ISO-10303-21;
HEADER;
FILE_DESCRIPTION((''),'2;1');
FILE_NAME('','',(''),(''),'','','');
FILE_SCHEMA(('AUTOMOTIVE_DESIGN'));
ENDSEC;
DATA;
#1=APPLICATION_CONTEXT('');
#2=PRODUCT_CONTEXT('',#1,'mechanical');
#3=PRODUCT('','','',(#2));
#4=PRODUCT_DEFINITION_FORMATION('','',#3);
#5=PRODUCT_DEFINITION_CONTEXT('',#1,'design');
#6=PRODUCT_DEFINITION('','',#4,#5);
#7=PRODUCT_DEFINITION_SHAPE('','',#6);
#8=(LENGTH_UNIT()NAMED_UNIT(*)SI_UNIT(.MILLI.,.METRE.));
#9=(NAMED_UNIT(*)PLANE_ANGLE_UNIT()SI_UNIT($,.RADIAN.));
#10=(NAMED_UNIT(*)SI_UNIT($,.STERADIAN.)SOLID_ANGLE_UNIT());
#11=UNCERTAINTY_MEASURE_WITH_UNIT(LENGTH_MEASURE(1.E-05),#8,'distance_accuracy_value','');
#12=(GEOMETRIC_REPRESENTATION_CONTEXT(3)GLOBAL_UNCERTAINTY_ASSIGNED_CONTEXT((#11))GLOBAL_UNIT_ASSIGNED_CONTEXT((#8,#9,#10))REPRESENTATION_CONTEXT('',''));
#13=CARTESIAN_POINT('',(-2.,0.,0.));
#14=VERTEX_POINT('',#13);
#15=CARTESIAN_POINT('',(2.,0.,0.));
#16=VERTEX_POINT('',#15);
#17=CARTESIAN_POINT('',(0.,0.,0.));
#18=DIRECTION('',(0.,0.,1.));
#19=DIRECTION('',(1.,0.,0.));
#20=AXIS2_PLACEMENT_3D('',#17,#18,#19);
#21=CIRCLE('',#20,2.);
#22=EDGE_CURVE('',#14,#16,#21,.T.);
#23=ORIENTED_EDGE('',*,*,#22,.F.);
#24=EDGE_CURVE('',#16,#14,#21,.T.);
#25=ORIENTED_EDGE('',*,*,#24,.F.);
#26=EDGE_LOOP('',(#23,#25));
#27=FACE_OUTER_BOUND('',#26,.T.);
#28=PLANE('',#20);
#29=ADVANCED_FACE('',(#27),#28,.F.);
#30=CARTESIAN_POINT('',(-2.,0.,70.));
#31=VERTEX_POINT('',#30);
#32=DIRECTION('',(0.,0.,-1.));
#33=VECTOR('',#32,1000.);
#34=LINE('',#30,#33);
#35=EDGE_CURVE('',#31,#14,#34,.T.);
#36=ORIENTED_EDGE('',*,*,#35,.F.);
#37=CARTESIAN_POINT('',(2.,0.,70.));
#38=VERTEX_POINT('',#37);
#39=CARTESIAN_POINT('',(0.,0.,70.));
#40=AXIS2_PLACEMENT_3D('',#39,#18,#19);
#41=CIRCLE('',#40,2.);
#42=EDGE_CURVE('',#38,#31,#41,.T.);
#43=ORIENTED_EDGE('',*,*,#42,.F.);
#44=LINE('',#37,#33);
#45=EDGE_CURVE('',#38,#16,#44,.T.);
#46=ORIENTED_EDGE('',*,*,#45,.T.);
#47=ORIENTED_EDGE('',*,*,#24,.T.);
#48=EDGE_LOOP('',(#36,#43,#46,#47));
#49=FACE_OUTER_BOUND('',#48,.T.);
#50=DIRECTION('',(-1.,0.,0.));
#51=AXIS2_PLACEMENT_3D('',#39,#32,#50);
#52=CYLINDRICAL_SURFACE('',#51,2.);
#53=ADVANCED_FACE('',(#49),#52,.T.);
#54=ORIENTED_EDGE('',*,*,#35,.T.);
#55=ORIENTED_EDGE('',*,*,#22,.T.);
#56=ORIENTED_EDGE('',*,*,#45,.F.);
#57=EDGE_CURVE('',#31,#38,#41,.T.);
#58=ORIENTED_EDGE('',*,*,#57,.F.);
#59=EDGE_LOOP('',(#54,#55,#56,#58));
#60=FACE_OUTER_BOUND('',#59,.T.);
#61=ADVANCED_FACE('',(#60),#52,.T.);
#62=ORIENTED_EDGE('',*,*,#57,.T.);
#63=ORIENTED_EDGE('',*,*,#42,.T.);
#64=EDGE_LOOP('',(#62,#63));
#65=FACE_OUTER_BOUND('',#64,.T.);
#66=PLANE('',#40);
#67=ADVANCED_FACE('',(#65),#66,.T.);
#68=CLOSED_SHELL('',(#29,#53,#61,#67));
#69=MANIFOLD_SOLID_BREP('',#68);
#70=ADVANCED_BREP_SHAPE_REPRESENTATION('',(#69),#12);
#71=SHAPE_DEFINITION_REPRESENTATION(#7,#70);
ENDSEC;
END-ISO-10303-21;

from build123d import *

# Parameters (mm, degrees)
SKETCH_1_R      = 2
EXTRUDE_1_DEPTH = 70


with BuildPart() as part:
    # 草图1 → 凸台-拉伸1 (new body)
    with BuildSketch(Plane.XY):
        Circle(SKETCH_1_R)
    extrude(amount=EXTRUDE_1_DEPTH)


solid = part.part
